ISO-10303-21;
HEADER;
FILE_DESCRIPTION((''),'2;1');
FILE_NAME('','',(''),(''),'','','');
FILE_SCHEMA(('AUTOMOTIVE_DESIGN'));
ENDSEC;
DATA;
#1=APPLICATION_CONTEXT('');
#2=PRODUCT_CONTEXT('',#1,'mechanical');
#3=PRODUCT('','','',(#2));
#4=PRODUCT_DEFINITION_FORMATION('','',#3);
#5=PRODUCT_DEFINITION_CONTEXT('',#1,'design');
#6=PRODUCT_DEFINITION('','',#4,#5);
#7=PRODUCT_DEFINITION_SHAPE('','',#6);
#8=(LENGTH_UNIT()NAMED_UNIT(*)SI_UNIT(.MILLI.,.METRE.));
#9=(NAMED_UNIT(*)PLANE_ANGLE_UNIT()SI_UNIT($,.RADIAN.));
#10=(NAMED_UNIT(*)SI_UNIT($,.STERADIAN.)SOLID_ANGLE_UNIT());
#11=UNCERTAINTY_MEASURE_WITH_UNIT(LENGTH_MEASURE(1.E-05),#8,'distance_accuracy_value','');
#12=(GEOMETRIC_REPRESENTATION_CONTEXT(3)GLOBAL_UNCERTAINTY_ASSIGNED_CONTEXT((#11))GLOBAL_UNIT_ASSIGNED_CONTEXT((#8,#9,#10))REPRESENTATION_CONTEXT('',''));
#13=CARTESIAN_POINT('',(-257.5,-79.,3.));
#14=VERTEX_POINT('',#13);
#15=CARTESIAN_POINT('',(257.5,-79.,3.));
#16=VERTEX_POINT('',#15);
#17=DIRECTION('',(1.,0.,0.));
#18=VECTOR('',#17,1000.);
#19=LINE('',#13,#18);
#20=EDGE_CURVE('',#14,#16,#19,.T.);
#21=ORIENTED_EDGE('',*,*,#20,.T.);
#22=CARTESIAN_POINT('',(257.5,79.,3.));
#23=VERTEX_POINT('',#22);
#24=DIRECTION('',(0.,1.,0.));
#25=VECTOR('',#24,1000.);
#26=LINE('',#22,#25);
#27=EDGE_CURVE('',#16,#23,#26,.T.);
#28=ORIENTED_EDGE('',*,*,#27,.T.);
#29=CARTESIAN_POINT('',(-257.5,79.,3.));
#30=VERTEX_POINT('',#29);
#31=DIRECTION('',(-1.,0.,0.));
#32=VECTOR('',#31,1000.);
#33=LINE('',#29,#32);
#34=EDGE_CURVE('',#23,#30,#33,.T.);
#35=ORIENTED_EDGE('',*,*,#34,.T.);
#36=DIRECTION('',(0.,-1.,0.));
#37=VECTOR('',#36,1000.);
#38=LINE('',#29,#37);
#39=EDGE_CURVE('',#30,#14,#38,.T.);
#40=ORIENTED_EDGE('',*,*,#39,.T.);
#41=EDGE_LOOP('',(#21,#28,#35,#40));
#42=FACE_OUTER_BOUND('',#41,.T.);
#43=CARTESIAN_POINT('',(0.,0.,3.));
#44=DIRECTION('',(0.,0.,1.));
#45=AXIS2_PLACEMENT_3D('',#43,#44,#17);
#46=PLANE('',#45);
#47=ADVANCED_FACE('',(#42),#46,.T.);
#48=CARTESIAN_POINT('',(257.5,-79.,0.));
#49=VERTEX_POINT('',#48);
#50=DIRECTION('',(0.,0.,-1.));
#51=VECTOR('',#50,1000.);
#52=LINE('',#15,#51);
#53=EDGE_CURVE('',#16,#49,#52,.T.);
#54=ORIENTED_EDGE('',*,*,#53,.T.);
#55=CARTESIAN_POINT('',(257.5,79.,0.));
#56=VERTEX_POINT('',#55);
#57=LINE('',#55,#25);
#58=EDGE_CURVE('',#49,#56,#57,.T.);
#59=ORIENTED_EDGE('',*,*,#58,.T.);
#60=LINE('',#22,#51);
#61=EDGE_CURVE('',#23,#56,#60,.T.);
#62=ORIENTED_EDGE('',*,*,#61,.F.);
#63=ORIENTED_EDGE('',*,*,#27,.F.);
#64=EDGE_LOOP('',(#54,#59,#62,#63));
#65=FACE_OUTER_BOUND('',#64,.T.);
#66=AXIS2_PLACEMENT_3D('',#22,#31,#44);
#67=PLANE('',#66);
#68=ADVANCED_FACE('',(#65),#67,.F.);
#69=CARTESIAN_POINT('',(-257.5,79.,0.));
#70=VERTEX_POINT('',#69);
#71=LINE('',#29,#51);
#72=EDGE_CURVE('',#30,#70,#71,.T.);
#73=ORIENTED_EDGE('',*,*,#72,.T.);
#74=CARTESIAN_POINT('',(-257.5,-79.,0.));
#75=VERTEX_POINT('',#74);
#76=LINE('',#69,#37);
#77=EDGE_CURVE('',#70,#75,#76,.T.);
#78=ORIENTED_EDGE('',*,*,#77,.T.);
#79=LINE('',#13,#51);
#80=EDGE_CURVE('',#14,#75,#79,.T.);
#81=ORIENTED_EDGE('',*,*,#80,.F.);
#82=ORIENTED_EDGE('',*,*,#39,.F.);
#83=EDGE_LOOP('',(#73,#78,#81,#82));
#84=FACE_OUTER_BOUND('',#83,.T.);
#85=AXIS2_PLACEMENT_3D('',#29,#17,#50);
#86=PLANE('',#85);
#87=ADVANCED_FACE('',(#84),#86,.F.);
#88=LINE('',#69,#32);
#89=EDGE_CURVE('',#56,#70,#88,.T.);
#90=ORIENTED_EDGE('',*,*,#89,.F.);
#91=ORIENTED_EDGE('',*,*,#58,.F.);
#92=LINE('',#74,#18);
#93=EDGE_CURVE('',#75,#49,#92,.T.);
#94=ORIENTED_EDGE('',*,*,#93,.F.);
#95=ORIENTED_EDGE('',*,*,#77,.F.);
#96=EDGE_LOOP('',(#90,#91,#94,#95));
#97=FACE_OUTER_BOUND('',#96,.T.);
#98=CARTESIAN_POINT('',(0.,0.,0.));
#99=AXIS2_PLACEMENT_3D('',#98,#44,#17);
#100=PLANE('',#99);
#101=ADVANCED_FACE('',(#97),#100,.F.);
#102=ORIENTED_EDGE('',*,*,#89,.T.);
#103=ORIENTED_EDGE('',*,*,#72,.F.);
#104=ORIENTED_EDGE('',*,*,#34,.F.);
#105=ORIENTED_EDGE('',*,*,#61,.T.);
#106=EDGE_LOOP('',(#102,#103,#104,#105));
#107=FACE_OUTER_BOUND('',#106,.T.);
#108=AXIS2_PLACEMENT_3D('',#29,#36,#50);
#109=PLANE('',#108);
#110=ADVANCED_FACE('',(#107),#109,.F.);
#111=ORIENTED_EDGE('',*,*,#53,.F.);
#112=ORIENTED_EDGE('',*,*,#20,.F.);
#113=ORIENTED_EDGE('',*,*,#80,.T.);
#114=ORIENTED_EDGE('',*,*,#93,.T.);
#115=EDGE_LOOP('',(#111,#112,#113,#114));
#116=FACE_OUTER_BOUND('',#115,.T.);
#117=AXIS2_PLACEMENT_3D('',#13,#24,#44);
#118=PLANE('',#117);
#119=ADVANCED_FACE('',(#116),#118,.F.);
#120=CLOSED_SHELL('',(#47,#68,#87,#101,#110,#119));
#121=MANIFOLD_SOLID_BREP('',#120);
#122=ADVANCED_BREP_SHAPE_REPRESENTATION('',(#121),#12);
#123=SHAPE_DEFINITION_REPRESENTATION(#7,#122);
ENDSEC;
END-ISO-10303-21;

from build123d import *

# Parameters (mm, degrees)
SKETCH1_W           = 515
SKETCH1_H           = 158
BOSS_EXTRUDE1_DEPTH = 3


with BuildPart() as part:
    # Sketch1 → Boss-Extrude1 (new body)
    with BuildSketch(Plane.XY):
        Rectangle(SKETCH1_W, SKETCH1_H)
    extrude(amount=BOSS_EXTRUDE1_DEPTH)


solid = part.part
